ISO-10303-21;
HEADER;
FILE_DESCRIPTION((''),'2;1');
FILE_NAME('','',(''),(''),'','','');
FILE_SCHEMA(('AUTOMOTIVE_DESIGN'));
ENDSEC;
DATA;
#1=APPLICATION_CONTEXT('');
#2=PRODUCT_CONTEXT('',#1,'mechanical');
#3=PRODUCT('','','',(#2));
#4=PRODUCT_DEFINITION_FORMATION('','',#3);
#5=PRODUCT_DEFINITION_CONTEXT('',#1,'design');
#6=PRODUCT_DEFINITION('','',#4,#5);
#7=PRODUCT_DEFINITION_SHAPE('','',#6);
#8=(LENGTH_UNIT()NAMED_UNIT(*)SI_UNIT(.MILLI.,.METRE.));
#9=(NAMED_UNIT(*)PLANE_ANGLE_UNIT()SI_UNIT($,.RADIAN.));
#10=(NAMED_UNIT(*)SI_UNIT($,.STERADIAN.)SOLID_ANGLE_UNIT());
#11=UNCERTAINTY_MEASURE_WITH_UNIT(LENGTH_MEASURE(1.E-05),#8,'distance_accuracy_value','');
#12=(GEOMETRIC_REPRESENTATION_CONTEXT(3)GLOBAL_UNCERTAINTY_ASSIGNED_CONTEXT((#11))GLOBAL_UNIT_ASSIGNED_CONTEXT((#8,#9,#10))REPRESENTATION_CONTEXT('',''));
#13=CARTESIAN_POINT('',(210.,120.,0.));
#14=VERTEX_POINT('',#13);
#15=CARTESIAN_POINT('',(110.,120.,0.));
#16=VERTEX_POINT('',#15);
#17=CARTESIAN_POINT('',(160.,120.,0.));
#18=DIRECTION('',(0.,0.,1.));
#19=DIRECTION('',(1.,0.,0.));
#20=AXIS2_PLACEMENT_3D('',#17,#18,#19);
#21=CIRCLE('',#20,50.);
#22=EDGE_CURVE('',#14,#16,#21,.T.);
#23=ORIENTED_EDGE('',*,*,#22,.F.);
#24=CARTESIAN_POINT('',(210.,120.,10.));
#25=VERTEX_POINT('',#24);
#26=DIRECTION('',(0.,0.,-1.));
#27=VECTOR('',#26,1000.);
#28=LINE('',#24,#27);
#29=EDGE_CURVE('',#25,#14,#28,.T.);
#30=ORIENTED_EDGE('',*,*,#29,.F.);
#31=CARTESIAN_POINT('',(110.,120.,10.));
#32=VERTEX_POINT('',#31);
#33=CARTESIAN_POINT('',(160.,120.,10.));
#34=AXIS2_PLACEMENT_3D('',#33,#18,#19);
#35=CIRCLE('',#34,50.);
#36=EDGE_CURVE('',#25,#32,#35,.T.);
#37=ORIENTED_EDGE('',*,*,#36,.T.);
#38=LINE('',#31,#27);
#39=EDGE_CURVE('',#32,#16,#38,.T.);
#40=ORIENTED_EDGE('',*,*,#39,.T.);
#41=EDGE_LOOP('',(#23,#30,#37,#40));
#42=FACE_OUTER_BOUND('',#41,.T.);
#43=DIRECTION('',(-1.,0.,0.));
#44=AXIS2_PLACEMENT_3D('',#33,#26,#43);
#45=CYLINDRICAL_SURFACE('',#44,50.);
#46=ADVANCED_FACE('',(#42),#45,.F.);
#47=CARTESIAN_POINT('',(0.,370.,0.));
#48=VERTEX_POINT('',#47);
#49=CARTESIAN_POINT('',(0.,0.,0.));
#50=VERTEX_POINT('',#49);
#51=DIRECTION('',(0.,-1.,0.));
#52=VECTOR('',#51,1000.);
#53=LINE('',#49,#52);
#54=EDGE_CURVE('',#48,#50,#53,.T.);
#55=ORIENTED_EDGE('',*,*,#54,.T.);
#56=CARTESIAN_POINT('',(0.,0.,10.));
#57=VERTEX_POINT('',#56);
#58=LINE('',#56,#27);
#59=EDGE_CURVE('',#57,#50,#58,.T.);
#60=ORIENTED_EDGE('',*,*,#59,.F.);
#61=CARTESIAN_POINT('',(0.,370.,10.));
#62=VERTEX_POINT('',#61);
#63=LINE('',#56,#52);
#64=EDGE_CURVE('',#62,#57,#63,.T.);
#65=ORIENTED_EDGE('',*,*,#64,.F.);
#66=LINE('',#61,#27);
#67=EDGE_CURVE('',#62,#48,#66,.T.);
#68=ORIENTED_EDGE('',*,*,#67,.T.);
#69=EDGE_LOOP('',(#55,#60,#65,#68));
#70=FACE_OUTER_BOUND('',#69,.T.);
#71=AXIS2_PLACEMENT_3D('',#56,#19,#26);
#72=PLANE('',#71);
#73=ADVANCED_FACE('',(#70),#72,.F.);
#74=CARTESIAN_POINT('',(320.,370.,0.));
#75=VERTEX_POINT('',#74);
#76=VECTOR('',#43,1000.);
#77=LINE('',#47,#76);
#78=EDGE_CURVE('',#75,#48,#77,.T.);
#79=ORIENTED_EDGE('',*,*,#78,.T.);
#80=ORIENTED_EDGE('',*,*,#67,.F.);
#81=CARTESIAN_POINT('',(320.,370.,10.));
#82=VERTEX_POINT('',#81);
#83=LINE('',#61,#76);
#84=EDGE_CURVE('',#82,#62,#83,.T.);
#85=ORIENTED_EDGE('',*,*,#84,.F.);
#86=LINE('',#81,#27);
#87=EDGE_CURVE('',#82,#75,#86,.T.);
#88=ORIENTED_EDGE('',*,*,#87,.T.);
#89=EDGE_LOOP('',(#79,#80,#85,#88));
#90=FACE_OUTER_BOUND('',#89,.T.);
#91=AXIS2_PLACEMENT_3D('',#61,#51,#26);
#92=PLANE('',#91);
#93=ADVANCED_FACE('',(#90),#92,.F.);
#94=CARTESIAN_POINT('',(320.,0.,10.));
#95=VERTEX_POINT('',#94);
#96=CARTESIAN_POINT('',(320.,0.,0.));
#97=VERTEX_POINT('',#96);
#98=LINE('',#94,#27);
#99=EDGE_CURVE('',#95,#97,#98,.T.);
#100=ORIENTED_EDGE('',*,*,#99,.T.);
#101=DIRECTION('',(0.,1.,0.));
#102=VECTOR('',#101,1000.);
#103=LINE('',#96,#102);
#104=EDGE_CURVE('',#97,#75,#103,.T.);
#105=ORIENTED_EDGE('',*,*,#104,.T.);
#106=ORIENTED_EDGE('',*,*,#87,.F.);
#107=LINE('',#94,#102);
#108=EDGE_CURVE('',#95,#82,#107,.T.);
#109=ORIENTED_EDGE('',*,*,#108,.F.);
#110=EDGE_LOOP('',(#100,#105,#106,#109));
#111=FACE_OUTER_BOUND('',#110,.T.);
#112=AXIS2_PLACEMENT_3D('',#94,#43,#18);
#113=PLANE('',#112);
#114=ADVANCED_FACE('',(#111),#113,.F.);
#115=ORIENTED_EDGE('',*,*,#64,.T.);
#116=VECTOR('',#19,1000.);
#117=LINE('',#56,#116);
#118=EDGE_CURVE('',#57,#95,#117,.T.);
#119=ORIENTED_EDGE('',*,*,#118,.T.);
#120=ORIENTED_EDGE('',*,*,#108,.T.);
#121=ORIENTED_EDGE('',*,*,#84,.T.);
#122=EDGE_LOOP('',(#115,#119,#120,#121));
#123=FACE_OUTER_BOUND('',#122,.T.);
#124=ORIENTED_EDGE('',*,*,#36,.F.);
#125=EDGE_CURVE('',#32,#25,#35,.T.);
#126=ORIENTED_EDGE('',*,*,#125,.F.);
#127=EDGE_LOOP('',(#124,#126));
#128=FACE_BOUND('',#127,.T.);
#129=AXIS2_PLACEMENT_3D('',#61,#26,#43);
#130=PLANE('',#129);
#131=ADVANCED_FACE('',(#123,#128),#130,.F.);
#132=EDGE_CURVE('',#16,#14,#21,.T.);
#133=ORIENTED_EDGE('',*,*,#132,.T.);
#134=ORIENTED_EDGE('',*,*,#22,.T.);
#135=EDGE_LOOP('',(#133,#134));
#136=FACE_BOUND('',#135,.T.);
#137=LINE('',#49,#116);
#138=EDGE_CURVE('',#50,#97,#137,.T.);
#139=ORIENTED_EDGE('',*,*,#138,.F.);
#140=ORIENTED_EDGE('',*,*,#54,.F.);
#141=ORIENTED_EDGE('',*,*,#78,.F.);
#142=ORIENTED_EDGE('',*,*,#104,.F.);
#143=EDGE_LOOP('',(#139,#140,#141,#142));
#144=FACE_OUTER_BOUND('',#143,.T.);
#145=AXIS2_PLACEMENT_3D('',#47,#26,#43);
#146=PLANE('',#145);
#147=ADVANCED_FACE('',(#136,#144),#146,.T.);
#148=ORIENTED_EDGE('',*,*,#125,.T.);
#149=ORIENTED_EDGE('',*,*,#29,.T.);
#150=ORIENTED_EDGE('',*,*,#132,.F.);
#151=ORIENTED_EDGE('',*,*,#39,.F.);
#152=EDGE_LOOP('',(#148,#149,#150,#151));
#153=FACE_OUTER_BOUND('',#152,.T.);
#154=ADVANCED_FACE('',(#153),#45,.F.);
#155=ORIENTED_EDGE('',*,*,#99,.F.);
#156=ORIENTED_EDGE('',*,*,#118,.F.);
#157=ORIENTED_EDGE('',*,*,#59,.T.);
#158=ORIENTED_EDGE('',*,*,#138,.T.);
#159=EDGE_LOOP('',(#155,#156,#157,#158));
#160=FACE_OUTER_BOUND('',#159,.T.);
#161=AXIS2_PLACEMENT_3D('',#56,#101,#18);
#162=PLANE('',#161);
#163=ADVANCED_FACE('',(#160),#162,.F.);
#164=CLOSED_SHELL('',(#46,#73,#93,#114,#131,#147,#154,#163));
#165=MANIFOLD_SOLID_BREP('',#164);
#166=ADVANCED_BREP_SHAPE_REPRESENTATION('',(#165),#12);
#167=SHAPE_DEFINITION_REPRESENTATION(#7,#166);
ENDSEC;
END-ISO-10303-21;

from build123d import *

# Parameters (mm, degrees)
SKETCH1_W           = 320
SKETCH1_H           = 370
SKETCH1_R           = 50
BOSS_EXTRUDE1_DEPTH = 10


with BuildPart() as part:
    # Sketch1 → Boss-Extrude1 (new body)
    with BuildSketch(Plane.XY):
        with Locations((160, 185)):
            Rectangle(SKETCH1_W, SKETCH1_H)
        with Locations((160, 120)):
            Circle(SKETCH1_R, mode=Mode.SUBTRACT)
    extrude(amount=BOSS_EXTRUDE1_DEPTH)


solid = part.part
